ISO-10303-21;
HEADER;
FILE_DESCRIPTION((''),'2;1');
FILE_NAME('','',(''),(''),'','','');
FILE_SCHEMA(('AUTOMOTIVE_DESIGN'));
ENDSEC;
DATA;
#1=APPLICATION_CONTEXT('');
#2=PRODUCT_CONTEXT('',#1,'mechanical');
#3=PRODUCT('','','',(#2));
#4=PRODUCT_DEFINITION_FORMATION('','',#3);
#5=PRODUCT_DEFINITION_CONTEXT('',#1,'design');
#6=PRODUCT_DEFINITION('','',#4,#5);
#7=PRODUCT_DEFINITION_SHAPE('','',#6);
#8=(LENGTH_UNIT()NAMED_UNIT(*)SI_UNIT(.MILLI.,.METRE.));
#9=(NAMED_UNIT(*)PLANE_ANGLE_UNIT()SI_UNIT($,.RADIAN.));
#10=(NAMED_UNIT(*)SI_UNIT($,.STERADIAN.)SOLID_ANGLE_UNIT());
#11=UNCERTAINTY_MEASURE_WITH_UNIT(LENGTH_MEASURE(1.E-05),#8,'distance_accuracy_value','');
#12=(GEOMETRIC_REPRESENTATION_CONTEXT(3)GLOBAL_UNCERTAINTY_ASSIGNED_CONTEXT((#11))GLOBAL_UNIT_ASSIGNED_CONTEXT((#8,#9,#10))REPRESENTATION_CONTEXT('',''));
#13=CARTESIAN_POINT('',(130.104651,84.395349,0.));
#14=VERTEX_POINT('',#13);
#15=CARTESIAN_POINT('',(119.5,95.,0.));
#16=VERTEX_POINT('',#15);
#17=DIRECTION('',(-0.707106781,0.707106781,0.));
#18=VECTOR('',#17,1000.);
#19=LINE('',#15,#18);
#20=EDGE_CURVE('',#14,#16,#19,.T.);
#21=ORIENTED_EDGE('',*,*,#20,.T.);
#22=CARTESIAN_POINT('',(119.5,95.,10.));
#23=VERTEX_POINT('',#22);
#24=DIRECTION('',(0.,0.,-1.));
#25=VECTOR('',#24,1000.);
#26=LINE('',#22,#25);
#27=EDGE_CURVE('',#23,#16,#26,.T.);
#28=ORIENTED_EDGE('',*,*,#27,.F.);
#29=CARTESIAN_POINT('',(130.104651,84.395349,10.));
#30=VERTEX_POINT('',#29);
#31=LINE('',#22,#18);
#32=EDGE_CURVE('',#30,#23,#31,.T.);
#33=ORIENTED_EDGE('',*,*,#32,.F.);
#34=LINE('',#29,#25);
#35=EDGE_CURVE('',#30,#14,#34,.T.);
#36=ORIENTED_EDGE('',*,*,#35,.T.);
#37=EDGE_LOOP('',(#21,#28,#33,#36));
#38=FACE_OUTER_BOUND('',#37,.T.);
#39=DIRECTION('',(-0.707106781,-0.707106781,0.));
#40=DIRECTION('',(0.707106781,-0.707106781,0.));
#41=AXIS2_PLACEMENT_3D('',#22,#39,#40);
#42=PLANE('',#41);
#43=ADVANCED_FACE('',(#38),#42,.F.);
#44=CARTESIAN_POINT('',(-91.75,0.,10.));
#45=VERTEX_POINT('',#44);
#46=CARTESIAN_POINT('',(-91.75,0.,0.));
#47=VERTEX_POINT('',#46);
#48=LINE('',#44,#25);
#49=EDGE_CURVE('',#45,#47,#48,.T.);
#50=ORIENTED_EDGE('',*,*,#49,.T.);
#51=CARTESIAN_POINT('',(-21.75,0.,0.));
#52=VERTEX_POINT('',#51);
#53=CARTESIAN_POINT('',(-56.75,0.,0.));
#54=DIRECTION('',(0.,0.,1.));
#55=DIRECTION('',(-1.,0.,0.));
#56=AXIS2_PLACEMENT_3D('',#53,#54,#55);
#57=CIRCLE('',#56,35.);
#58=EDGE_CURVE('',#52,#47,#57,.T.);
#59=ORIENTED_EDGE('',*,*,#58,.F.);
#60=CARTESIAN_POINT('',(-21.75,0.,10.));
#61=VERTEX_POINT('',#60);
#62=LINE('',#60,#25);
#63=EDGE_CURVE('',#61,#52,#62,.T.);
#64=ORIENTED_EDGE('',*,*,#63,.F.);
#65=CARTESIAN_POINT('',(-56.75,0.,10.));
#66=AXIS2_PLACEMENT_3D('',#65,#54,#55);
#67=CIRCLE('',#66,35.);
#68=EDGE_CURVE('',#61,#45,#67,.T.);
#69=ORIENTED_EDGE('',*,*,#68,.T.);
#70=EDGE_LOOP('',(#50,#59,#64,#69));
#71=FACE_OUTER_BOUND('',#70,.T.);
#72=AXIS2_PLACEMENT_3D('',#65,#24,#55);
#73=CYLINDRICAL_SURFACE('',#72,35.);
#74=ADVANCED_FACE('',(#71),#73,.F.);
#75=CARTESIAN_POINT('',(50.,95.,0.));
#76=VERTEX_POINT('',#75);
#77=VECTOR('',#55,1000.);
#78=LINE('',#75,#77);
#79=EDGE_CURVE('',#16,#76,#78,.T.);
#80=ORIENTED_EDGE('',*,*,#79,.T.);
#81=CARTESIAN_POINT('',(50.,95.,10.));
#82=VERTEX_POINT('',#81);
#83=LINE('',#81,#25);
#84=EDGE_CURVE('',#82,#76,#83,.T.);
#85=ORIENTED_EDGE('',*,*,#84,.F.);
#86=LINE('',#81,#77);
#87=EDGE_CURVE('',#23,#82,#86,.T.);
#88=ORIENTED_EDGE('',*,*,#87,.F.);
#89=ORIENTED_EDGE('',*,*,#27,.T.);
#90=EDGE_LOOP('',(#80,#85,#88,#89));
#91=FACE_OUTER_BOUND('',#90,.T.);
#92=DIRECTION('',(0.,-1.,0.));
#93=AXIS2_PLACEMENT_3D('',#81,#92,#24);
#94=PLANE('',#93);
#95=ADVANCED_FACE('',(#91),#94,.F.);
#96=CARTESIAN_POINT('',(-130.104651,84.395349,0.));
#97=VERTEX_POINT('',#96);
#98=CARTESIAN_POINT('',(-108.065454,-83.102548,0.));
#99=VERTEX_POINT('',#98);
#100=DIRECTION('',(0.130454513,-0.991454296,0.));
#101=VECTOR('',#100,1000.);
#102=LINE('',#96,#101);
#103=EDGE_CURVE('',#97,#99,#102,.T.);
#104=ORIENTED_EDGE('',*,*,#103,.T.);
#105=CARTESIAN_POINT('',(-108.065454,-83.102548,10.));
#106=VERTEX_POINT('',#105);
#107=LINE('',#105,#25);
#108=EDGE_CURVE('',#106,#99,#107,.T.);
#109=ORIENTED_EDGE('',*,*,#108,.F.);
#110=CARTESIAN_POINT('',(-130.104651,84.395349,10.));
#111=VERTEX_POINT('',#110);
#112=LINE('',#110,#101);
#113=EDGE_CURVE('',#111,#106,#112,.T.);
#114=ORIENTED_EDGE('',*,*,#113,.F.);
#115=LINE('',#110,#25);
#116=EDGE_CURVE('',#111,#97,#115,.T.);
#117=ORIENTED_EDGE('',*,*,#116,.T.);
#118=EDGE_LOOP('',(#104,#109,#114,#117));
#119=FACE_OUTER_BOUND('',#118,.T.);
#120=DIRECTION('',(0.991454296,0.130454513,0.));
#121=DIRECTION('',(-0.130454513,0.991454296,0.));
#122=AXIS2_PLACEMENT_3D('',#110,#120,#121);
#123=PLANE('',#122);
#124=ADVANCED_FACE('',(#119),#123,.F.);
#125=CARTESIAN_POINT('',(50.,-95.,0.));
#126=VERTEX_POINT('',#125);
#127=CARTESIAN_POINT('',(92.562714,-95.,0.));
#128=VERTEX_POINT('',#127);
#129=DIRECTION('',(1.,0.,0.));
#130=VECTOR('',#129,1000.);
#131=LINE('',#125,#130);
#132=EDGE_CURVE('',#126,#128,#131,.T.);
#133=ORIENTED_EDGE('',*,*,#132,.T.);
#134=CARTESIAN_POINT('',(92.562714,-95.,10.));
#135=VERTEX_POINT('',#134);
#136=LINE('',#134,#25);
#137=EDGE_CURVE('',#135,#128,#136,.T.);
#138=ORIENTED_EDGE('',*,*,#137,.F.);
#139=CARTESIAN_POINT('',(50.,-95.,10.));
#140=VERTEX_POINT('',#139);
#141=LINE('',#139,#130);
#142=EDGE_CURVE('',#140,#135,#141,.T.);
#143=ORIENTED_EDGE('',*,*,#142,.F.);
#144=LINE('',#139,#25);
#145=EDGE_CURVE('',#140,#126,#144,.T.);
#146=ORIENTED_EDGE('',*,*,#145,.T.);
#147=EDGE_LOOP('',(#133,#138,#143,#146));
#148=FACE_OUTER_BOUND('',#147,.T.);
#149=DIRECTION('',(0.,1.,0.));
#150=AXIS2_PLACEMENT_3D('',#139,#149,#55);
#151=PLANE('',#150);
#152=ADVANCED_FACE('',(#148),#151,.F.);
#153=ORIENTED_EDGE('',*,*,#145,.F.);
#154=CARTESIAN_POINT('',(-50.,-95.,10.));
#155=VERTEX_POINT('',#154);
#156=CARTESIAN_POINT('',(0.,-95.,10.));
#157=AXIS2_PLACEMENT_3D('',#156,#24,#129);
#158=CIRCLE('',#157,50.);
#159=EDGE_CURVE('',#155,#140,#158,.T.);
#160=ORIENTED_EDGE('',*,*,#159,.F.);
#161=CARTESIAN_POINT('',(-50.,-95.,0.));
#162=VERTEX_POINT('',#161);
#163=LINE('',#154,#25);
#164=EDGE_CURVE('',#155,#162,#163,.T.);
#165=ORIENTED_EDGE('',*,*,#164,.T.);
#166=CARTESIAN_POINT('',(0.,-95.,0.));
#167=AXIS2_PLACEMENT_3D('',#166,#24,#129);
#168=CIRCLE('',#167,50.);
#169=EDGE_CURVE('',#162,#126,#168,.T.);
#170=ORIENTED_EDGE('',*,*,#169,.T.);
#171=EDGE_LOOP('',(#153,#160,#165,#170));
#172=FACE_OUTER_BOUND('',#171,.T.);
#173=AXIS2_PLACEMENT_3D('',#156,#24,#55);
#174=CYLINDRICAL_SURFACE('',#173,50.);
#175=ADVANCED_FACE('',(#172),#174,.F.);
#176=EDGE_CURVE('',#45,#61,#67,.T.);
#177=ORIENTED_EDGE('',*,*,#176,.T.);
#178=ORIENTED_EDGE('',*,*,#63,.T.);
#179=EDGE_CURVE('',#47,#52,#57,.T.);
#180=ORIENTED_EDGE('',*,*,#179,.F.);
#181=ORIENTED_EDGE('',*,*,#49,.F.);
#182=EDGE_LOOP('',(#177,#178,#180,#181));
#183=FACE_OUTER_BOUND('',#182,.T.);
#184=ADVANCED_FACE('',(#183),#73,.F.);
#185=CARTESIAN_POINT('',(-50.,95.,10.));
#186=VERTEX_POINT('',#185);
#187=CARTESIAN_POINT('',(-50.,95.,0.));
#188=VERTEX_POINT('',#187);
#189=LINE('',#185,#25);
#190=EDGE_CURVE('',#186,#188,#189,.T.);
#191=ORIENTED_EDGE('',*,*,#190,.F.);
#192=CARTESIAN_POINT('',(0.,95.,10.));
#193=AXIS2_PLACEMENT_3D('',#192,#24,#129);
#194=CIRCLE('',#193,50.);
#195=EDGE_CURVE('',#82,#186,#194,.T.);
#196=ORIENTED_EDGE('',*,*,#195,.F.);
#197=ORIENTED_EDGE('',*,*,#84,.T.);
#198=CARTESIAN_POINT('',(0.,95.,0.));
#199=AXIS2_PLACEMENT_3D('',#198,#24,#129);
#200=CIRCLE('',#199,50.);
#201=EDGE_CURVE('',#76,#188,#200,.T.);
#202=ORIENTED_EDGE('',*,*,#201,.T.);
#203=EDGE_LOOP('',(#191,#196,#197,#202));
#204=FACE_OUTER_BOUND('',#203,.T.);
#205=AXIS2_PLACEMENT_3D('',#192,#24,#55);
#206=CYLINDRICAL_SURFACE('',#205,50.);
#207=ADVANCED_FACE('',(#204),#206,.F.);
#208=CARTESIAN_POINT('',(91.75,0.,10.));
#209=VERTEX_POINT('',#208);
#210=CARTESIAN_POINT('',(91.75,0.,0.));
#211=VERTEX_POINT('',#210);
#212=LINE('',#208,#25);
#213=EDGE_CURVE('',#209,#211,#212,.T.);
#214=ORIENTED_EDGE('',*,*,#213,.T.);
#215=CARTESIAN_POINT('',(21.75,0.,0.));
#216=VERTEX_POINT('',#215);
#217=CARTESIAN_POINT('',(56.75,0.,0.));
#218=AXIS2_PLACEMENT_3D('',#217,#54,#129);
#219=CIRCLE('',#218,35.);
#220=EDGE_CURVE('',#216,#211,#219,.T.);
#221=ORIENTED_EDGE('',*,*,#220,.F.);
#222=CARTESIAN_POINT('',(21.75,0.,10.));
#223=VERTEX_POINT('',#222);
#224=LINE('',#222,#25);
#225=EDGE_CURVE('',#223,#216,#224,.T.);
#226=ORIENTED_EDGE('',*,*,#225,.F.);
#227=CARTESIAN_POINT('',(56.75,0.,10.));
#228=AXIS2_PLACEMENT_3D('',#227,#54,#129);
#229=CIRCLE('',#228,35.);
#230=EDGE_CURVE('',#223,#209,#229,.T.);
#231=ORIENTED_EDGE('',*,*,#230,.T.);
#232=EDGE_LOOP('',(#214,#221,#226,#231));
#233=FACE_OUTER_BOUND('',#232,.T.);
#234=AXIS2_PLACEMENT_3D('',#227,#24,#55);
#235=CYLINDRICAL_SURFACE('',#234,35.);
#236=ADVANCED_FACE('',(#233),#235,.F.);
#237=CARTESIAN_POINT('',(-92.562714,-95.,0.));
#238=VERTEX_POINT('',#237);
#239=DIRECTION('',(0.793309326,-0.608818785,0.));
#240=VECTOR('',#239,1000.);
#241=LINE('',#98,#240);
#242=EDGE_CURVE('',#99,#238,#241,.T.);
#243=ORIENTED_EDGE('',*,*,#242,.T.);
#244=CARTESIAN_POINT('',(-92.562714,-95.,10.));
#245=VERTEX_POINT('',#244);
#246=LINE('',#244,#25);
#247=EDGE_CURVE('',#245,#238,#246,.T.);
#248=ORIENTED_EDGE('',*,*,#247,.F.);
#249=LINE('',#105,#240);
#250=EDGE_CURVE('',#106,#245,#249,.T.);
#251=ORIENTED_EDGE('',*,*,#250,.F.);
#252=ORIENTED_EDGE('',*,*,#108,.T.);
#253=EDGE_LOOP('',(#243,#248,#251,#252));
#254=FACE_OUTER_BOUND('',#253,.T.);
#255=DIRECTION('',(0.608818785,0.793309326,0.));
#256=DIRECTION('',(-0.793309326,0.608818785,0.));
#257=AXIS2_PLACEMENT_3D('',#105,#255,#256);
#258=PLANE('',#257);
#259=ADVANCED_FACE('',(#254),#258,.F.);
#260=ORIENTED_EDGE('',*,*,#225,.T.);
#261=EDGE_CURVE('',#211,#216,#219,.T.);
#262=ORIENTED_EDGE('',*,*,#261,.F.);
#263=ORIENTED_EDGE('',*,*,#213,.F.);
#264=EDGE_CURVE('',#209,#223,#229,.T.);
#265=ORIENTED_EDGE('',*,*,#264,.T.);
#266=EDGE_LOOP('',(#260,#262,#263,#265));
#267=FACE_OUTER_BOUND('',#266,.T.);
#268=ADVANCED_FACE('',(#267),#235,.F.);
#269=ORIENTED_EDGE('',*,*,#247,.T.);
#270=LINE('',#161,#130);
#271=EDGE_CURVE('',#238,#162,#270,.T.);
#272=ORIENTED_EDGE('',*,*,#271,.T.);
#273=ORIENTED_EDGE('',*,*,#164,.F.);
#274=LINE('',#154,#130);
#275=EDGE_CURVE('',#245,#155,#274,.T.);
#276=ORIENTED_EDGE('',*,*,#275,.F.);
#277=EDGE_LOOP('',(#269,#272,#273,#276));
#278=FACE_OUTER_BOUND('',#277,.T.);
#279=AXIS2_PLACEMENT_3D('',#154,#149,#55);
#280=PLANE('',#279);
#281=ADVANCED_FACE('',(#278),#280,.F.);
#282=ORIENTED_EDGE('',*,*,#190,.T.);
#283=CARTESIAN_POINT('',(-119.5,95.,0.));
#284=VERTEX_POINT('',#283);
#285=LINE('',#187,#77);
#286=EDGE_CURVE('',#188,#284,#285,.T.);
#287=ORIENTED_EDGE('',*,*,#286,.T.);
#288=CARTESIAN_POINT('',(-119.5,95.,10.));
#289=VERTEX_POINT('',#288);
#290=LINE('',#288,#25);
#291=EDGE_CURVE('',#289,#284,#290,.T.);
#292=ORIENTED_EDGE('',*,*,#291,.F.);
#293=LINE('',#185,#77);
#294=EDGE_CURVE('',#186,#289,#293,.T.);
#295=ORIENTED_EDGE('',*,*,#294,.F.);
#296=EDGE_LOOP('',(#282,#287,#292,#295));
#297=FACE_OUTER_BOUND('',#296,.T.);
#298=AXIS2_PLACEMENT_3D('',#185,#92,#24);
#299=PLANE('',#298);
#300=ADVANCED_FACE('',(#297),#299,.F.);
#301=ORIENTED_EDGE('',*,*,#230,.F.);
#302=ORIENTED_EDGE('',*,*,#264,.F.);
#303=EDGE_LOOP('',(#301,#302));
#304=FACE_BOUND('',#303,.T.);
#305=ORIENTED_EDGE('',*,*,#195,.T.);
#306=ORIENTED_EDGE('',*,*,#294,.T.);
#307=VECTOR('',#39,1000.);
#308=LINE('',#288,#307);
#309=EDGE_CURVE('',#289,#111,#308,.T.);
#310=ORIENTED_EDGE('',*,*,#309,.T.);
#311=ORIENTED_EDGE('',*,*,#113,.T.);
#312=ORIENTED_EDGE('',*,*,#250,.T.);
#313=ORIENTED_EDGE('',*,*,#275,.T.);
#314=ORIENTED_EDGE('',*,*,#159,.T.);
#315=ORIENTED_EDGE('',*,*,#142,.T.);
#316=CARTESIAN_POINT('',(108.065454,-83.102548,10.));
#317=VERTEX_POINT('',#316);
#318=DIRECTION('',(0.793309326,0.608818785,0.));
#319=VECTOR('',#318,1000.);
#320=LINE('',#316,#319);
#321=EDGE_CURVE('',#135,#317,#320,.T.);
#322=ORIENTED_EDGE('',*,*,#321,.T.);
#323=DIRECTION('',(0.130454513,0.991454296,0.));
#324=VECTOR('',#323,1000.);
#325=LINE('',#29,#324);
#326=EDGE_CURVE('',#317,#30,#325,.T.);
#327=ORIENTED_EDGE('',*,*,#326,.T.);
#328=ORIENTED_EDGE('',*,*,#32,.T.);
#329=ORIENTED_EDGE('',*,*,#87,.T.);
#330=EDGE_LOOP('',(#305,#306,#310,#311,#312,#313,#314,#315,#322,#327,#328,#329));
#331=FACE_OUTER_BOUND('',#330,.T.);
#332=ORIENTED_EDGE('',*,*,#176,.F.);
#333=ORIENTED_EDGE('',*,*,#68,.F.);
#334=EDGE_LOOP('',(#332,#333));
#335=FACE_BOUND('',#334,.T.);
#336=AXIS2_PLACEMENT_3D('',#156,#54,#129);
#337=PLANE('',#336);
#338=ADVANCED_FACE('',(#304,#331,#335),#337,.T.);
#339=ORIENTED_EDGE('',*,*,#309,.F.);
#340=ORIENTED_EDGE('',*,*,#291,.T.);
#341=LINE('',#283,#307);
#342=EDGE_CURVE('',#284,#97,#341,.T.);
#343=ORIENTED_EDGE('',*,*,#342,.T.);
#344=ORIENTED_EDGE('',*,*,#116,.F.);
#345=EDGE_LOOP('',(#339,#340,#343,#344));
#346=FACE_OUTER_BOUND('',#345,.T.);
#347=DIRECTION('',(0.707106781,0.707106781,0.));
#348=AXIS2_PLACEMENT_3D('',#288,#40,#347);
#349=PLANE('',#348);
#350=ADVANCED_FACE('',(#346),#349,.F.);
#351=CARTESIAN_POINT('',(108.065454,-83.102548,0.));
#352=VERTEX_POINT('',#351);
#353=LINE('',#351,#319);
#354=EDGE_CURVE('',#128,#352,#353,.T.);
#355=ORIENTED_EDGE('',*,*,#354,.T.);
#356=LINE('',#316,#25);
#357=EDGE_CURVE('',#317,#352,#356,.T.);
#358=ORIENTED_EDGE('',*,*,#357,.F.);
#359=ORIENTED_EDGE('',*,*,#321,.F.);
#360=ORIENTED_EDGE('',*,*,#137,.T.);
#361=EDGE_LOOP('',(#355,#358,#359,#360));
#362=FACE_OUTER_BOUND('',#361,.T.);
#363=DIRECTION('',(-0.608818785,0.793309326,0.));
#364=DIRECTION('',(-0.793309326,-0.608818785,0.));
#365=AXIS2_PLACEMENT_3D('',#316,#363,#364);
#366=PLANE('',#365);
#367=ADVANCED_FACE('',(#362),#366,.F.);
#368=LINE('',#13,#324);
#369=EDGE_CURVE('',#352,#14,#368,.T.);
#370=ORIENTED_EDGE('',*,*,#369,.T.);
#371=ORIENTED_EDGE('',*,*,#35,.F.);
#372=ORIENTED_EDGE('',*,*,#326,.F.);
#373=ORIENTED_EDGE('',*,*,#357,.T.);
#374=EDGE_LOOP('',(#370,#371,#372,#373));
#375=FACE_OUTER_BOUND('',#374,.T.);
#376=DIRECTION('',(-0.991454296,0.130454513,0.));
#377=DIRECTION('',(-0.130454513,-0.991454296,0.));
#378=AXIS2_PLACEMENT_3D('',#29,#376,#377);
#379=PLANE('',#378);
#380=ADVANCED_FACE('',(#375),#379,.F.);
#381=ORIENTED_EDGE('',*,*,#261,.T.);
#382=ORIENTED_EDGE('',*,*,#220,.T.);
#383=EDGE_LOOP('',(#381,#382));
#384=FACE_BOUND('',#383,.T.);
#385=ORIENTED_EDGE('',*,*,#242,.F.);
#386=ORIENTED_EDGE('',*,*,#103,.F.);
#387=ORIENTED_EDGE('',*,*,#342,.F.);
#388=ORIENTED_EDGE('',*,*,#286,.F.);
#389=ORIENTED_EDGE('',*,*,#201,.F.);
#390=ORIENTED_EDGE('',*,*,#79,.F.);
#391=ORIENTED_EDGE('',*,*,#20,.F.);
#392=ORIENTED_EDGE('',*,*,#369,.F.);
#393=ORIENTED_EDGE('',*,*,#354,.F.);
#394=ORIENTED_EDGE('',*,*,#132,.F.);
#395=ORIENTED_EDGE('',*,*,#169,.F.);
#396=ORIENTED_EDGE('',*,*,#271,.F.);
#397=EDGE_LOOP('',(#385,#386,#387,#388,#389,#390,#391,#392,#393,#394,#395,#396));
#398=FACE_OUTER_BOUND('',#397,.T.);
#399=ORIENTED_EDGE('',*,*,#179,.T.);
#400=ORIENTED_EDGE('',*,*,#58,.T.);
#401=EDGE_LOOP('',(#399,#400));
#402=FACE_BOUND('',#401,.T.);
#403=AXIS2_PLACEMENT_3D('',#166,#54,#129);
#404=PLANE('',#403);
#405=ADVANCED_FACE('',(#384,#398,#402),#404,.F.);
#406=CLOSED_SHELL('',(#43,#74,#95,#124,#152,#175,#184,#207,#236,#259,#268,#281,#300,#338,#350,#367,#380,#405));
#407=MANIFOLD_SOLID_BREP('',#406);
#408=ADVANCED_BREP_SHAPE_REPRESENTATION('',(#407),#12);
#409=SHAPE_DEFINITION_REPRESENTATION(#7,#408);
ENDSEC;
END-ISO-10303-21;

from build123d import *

# Parameters (mm, degrees)
SKETCH1_R           = 35
BOSS_EXTRUDE1_DEPTH = 10


with BuildPart() as part:
    # Sketch1 → Boss-Extrude1 (new body)
    with BuildSketch(Plane.XY):
        with BuildLine():
            Line((50, 95), (119.5, 95))
            Line((119.5, 95), (130.104651163, 84.395348837))
            Line((130.104651163, 84.395348837), (108.065454151, -83.102548453))
            Line((108.065454151, -83.102548453), (92.562714257, -95))
            Line((92.562714257, -95), (50, -95))
            ThreePointArc((50, -95), (0, -45), (-50, -95))
            Line((-50, -95), (-92.562714257, -95))
            Line((-92.562714257, -95), (-108.065454151, -83.102548453))
            Line((-108.065454151, -83.102548453), (-130.104651163, 84.395348837))
            Line((-130.104651163, 84.395348837), (-119.5, 95))
            Line((-119.5, 95), (-50, 95))
            ThreePointArc((-50, 95), (0, 45), (50, 95))
        make_face()
        with Locations((56.75, 0)):
            Circle(SKETCH1_R, mode=Mode.SUBTRACT)
        with Locations(Location((-56.75, 0, 0), (0, 0, 180))):
            Circle(SKETCH1_R, mode=Mode.SUBTRACT)
    extrude(amount=BOSS_EXTRUDE1_DEPTH)


solid = part.part
